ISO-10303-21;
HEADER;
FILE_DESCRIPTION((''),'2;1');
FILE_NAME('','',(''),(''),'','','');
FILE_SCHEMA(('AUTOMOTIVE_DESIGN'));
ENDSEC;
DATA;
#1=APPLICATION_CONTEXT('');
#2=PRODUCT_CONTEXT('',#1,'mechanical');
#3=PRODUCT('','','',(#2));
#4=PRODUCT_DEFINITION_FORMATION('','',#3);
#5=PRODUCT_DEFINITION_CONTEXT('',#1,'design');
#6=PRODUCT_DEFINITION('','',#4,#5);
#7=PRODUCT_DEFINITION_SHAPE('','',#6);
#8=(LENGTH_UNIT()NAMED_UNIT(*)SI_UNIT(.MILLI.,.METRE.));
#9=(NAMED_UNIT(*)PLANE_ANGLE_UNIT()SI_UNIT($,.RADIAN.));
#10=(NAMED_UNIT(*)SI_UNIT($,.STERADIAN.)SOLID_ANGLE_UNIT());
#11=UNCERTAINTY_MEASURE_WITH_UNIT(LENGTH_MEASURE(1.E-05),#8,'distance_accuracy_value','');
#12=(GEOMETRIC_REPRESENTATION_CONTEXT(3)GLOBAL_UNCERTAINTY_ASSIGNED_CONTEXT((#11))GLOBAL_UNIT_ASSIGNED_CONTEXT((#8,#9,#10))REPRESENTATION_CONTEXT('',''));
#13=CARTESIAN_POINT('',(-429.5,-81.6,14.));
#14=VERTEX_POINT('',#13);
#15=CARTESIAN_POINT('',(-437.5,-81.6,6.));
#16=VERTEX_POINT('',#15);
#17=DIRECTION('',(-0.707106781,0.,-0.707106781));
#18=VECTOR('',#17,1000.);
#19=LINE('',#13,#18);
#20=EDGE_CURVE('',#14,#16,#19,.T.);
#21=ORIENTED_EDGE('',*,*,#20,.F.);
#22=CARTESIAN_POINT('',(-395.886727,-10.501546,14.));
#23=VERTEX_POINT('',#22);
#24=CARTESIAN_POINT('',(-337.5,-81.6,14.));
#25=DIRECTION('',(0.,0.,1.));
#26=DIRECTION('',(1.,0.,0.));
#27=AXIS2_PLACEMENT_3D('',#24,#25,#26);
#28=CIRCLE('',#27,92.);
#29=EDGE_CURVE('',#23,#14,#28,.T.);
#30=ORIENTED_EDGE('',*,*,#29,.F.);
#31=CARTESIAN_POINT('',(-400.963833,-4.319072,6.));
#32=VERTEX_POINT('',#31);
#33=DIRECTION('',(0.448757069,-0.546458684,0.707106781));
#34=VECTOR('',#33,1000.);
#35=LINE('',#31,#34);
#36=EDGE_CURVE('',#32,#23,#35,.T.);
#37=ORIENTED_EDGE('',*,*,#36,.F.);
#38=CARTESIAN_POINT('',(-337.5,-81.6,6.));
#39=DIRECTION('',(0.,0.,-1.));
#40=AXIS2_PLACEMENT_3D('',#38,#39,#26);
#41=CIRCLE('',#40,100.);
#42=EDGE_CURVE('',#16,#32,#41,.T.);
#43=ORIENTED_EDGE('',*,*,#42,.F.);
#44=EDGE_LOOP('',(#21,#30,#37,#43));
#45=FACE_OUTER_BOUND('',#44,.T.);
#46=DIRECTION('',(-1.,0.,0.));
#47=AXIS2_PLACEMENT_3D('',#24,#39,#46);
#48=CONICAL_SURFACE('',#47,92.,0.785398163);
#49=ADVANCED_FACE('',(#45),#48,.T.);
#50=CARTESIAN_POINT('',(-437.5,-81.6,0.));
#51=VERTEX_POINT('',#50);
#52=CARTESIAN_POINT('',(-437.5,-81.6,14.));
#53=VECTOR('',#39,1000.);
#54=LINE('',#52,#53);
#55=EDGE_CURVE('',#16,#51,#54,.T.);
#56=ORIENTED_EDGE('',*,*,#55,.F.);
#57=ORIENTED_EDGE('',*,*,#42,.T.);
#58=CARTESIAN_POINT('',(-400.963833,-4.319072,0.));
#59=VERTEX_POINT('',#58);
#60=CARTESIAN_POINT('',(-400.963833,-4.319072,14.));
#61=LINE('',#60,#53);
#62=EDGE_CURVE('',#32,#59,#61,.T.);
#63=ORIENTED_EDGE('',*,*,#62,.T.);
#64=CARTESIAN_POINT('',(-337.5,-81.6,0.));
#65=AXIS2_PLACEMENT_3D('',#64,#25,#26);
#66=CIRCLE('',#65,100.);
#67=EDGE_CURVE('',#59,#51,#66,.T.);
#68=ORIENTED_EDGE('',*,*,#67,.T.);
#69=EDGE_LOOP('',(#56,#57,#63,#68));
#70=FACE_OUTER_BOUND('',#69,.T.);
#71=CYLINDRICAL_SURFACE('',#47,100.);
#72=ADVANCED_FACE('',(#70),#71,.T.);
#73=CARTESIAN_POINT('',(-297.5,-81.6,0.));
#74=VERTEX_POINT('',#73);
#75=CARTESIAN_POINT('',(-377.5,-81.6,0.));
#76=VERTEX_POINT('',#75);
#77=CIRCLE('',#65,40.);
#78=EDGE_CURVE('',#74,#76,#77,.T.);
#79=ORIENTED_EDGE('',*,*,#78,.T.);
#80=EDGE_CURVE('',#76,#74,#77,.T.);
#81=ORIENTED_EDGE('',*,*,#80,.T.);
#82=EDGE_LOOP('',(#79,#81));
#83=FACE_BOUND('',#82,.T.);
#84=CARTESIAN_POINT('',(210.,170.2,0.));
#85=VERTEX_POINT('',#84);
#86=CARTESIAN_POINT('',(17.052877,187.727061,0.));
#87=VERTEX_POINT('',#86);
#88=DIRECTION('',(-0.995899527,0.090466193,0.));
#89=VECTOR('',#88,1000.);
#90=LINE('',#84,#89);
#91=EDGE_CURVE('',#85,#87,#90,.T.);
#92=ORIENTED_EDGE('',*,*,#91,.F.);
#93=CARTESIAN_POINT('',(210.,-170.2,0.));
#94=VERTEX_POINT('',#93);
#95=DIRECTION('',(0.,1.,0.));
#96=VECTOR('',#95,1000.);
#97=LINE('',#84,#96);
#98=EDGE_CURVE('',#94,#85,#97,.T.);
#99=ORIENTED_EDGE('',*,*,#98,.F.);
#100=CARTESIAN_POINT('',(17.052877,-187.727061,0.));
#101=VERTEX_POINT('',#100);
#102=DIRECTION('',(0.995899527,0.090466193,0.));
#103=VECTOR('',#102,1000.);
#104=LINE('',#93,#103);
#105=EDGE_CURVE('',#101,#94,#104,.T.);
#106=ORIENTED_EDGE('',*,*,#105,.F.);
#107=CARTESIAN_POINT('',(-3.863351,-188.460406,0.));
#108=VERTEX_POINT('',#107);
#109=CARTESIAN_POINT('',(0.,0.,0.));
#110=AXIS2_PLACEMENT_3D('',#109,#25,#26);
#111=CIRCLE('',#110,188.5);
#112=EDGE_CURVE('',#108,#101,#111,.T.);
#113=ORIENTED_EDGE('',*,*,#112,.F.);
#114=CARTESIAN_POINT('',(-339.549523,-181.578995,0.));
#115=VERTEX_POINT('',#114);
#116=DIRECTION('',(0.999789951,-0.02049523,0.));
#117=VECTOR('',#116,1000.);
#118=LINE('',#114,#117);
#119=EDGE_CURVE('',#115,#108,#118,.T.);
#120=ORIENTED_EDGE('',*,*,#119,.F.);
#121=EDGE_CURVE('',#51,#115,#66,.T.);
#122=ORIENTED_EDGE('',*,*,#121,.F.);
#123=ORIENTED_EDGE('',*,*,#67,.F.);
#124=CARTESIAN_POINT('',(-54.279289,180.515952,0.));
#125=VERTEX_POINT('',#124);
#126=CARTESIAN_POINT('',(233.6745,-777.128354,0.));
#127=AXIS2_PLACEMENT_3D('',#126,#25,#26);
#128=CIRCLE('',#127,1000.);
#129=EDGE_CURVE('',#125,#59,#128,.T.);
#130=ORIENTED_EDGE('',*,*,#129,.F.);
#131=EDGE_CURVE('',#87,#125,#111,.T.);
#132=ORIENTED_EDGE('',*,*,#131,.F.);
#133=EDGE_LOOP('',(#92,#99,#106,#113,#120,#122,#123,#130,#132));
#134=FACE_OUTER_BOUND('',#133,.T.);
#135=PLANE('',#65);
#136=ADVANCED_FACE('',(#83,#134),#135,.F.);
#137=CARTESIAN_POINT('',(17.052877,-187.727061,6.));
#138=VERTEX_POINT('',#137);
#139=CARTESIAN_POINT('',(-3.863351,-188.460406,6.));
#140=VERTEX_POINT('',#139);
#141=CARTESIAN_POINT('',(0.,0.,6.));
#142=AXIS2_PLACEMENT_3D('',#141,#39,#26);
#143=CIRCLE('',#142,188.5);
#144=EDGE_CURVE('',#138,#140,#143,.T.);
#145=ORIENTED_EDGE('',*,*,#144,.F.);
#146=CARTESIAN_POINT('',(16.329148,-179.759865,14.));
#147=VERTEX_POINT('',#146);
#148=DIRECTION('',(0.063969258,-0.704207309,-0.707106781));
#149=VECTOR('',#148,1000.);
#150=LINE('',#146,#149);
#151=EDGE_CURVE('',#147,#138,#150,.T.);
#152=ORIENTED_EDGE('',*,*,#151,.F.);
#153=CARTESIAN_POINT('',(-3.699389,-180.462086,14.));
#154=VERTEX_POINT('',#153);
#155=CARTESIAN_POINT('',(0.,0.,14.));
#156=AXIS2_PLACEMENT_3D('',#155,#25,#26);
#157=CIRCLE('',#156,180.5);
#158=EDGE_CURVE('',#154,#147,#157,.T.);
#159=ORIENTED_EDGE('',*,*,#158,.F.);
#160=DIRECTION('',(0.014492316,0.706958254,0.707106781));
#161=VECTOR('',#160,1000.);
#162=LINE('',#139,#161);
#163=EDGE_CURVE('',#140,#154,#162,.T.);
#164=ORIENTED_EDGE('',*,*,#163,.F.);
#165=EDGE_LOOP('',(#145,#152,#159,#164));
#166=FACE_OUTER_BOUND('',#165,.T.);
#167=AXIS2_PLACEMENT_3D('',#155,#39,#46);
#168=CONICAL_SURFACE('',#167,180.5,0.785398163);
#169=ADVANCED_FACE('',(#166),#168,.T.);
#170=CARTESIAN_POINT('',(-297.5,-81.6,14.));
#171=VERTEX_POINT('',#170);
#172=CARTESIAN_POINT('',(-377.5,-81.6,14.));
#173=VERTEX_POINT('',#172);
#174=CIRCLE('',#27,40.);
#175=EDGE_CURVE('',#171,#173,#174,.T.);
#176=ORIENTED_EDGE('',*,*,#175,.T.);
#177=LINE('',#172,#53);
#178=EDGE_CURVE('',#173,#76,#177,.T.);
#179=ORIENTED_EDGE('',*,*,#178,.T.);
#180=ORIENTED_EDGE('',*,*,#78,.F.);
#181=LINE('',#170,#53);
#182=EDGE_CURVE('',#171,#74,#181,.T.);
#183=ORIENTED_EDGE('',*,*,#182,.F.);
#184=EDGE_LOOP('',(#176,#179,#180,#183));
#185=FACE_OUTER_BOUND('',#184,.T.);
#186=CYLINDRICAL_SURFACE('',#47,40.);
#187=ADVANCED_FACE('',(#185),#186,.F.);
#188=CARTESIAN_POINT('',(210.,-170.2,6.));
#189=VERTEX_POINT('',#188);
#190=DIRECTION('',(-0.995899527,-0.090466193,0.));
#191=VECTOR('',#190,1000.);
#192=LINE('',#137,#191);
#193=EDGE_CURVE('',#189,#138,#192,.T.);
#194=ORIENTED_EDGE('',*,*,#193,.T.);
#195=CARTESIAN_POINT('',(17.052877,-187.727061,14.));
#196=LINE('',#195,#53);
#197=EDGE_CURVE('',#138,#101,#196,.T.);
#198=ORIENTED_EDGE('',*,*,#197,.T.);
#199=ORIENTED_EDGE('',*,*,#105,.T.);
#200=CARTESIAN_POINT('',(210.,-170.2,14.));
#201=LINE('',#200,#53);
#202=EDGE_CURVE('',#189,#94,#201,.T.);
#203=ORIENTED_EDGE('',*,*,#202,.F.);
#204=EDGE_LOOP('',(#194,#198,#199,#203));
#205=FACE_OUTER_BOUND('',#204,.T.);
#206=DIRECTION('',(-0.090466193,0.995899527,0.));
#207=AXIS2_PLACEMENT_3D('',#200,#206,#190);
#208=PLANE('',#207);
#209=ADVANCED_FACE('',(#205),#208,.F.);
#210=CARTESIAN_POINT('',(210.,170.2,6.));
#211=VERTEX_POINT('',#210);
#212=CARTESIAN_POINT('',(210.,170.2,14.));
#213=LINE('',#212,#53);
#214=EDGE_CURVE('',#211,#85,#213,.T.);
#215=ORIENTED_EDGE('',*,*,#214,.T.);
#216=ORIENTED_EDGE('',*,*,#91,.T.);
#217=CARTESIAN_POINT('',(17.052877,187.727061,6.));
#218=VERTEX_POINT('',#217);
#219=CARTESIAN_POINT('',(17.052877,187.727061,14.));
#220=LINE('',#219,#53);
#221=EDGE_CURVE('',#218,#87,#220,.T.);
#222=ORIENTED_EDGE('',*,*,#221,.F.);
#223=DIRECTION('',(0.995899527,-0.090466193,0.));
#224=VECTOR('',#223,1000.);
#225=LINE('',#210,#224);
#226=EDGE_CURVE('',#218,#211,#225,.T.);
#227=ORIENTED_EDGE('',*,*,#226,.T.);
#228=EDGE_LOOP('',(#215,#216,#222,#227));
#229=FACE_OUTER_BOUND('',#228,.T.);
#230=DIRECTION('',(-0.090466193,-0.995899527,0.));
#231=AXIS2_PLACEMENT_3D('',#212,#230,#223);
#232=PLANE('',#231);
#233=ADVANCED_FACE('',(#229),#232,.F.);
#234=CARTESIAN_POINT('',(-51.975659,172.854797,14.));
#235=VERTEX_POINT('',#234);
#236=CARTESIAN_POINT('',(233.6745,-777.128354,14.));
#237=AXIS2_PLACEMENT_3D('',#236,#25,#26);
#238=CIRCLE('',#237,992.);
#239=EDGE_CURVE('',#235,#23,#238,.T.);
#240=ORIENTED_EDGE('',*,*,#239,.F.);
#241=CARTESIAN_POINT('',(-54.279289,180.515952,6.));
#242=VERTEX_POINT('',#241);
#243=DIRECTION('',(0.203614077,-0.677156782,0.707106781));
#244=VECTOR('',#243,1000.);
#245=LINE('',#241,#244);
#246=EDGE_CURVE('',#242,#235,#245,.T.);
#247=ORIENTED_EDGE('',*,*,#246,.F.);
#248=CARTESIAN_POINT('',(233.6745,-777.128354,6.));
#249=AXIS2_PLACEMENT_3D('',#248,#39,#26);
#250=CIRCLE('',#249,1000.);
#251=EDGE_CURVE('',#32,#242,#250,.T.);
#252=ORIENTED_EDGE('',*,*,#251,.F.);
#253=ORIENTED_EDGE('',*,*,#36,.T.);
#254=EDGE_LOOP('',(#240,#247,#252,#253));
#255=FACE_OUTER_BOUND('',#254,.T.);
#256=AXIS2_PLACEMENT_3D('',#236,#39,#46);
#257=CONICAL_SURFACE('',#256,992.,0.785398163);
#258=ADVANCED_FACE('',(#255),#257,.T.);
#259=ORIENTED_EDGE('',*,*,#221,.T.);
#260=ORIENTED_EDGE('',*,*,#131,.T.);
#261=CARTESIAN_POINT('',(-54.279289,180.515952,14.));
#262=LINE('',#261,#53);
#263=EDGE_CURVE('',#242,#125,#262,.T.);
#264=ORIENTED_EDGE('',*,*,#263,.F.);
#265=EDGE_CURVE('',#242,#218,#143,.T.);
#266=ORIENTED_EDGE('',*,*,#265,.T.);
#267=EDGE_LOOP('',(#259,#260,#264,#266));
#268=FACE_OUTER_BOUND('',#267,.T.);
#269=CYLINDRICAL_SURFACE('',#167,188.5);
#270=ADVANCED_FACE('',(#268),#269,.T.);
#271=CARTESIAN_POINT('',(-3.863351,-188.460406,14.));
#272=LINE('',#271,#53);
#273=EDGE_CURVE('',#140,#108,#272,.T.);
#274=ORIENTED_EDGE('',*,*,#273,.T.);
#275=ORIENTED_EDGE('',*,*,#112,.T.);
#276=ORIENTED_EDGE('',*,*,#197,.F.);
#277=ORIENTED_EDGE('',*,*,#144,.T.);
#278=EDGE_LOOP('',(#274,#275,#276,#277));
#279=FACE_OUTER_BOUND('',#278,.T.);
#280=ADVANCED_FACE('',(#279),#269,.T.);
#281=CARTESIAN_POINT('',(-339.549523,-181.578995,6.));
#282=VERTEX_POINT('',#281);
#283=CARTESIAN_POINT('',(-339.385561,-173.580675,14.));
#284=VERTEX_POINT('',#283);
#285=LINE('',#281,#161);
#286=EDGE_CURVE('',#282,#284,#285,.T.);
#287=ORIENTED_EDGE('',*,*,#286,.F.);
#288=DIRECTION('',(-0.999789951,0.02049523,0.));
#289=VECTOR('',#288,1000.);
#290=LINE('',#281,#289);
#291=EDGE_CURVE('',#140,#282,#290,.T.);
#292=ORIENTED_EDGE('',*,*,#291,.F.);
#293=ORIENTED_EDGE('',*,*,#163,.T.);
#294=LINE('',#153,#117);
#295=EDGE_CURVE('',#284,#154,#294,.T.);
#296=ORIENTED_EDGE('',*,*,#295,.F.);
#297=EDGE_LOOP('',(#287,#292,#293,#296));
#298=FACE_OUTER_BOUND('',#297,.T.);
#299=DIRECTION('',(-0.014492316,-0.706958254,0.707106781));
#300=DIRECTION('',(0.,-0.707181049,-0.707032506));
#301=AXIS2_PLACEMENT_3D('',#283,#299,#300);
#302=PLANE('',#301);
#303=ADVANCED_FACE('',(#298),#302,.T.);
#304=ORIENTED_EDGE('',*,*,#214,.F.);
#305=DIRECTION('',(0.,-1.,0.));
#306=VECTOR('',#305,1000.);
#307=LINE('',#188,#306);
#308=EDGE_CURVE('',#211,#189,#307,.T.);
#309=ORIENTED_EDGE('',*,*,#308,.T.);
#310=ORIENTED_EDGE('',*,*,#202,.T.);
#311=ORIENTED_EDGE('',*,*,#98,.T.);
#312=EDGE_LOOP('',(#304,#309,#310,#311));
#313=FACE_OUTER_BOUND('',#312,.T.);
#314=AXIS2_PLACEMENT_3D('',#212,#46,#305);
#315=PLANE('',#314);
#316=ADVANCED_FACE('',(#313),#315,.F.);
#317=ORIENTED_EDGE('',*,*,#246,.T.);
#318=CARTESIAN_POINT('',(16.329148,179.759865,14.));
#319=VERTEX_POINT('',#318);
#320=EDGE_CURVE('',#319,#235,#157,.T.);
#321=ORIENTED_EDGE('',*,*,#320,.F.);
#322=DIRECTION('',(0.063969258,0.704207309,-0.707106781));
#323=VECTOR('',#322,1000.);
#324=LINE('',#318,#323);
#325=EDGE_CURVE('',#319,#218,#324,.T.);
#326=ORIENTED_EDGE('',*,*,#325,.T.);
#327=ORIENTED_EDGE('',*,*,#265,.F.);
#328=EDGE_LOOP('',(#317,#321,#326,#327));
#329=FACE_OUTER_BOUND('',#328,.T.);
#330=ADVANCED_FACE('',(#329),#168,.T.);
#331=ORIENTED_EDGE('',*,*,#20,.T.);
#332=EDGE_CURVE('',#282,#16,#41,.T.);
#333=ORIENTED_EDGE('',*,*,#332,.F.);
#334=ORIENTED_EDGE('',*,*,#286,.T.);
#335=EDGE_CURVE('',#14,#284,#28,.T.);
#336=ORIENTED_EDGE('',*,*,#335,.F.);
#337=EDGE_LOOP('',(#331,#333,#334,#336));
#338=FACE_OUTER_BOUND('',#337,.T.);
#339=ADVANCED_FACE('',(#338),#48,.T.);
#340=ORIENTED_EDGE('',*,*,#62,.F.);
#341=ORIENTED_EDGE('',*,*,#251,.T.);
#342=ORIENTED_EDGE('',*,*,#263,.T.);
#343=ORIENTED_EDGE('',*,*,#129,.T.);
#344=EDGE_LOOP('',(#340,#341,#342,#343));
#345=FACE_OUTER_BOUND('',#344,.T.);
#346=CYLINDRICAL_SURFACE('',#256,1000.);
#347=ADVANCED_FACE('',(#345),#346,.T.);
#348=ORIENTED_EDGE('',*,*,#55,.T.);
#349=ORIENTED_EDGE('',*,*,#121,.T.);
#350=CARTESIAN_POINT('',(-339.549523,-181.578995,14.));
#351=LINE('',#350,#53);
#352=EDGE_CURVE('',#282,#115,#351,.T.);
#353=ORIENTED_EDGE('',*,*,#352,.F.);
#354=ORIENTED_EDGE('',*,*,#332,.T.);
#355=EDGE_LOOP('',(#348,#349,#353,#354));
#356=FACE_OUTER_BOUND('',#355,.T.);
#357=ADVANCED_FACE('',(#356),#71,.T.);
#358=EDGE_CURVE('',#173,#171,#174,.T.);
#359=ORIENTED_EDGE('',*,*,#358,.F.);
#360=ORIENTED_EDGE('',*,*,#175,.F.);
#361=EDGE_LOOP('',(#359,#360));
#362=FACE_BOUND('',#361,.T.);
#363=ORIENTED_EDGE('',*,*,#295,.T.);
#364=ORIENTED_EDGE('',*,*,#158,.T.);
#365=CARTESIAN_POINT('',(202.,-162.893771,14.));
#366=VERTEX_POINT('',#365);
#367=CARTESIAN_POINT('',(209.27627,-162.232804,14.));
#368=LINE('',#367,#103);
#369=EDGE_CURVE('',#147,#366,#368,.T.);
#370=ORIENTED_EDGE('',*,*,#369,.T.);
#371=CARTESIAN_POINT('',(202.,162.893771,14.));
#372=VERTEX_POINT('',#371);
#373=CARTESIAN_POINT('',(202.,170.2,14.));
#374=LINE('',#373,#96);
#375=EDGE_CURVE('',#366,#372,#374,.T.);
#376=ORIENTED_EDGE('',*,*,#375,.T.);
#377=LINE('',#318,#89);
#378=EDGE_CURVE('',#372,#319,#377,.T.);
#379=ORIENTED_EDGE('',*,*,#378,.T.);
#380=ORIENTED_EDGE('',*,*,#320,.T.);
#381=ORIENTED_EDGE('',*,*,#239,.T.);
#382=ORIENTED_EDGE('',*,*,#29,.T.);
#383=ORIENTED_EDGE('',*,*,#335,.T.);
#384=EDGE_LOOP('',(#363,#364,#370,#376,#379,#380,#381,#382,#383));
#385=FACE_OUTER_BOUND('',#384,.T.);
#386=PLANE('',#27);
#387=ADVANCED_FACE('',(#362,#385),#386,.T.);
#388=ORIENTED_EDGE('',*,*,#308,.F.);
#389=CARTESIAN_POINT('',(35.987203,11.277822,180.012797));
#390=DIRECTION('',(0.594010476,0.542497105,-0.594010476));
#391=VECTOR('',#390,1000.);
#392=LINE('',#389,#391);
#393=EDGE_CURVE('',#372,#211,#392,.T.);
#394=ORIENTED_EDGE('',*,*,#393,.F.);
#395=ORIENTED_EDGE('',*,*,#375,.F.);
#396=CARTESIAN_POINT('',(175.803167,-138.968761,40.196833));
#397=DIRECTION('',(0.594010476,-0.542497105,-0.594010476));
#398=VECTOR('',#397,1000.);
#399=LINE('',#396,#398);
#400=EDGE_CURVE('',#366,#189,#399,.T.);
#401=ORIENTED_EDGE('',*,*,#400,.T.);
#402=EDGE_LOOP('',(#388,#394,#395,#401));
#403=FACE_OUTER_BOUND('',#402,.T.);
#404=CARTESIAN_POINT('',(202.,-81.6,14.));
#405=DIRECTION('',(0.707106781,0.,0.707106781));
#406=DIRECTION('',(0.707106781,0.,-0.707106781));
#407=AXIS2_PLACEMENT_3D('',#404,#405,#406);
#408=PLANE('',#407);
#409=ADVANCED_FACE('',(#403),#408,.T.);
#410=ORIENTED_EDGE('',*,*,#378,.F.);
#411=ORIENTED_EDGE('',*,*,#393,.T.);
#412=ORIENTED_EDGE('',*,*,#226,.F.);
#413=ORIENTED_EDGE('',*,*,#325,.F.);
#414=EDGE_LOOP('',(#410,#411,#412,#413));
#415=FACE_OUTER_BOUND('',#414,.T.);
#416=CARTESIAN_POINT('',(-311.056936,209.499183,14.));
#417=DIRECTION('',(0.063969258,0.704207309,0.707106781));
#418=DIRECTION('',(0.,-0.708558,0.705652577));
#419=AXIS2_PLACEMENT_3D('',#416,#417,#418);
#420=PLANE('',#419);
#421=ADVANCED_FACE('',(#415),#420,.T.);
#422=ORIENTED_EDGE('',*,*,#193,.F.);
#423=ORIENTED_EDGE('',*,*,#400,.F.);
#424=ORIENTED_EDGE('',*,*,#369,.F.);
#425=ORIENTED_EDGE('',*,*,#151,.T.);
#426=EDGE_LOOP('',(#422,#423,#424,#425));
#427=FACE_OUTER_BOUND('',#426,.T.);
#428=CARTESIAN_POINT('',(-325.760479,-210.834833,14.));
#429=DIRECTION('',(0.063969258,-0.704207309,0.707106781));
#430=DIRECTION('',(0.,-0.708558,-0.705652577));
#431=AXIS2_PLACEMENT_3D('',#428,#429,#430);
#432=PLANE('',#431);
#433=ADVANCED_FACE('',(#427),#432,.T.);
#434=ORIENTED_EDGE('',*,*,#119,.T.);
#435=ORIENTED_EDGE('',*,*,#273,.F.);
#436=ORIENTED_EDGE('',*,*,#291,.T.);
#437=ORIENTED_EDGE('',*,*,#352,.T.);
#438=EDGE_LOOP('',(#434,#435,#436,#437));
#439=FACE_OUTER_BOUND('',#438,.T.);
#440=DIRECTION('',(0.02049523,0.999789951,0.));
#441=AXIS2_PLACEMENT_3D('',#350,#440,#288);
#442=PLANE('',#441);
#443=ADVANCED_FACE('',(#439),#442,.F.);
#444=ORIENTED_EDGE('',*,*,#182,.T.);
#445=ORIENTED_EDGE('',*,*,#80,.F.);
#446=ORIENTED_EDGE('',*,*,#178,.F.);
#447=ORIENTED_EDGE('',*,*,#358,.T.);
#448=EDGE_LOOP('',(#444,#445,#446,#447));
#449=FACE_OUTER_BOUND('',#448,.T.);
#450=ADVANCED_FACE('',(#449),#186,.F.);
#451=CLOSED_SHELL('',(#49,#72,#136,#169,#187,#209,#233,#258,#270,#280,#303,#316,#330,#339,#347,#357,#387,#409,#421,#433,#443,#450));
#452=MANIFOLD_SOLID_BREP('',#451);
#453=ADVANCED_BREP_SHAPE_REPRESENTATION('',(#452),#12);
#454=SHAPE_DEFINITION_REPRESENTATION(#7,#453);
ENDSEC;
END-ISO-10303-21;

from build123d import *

# Parameters (mm, degrees)
SKETCH1_R           = 40
BOSS_EXTRUDE1_DEPTH = 14
CHAMFER1_SIZE       = 8


with BuildPart() as part:
    # Sketch1 → Boss-Extrude1 (new body)
    with BuildSketch(Plane.XY):
        with BuildLine():
            Line((210, 170.2), (17.052877352, 187.727060846))
            ThreePointArc((17.052877352, 187.727060846), (-18.959205139, 187.54412425), (-54.27928922, 180.515951544))
            ThreePointArc((-54.27928922, 180.515951544), (-236.788094268, 105.291584642), (-400.963833305, -4.319071808))
            ThreePointArc((-400.963833305, -4.319071808), (-431.989523554, -114.33728667), (-339.549522969, -181.578995072))
            Line((-339.549522969, -181.578995072), (-3.863350797, -188.460405711))
            ThreePointArc((-3.863350797, -188.460405711), (6.604949005, -188.384247347), (17.052877352, -187.727060846))
            Line((17.052877352, -187.727060846), (210, -170.2))
            Line((210, -170.2), (210, 170.2))
        make_face()
        with Locations((-337.5, -81.6)):
            Circle(SKETCH1_R, mode=Mode.SUBTRACT)
    extrude(amount=BOSS_EXTRUDE1_DEPTH)

    # Chamfer1
    chamfer1_edges = [part.edges().sort_by_distance(p)[0] for p in [
        (6.604949005, -188.384247347, 14),
        (113.526438676, -178.963530423, 14),
        (210, 0, 14),
        (113.526438676, 178.963530423, 14),
        (-18.959205139, 187.54412425, 14),
        (-236.788094268, 105.291584642, 14),
        (-431.989523554, -114.33728667, 14),
        (-171.706436883, -185.019700391, 14),
    ]]
    chamfer(chamfer1_edges, length=CHAMFER1_SIZE)


solid = part.part
